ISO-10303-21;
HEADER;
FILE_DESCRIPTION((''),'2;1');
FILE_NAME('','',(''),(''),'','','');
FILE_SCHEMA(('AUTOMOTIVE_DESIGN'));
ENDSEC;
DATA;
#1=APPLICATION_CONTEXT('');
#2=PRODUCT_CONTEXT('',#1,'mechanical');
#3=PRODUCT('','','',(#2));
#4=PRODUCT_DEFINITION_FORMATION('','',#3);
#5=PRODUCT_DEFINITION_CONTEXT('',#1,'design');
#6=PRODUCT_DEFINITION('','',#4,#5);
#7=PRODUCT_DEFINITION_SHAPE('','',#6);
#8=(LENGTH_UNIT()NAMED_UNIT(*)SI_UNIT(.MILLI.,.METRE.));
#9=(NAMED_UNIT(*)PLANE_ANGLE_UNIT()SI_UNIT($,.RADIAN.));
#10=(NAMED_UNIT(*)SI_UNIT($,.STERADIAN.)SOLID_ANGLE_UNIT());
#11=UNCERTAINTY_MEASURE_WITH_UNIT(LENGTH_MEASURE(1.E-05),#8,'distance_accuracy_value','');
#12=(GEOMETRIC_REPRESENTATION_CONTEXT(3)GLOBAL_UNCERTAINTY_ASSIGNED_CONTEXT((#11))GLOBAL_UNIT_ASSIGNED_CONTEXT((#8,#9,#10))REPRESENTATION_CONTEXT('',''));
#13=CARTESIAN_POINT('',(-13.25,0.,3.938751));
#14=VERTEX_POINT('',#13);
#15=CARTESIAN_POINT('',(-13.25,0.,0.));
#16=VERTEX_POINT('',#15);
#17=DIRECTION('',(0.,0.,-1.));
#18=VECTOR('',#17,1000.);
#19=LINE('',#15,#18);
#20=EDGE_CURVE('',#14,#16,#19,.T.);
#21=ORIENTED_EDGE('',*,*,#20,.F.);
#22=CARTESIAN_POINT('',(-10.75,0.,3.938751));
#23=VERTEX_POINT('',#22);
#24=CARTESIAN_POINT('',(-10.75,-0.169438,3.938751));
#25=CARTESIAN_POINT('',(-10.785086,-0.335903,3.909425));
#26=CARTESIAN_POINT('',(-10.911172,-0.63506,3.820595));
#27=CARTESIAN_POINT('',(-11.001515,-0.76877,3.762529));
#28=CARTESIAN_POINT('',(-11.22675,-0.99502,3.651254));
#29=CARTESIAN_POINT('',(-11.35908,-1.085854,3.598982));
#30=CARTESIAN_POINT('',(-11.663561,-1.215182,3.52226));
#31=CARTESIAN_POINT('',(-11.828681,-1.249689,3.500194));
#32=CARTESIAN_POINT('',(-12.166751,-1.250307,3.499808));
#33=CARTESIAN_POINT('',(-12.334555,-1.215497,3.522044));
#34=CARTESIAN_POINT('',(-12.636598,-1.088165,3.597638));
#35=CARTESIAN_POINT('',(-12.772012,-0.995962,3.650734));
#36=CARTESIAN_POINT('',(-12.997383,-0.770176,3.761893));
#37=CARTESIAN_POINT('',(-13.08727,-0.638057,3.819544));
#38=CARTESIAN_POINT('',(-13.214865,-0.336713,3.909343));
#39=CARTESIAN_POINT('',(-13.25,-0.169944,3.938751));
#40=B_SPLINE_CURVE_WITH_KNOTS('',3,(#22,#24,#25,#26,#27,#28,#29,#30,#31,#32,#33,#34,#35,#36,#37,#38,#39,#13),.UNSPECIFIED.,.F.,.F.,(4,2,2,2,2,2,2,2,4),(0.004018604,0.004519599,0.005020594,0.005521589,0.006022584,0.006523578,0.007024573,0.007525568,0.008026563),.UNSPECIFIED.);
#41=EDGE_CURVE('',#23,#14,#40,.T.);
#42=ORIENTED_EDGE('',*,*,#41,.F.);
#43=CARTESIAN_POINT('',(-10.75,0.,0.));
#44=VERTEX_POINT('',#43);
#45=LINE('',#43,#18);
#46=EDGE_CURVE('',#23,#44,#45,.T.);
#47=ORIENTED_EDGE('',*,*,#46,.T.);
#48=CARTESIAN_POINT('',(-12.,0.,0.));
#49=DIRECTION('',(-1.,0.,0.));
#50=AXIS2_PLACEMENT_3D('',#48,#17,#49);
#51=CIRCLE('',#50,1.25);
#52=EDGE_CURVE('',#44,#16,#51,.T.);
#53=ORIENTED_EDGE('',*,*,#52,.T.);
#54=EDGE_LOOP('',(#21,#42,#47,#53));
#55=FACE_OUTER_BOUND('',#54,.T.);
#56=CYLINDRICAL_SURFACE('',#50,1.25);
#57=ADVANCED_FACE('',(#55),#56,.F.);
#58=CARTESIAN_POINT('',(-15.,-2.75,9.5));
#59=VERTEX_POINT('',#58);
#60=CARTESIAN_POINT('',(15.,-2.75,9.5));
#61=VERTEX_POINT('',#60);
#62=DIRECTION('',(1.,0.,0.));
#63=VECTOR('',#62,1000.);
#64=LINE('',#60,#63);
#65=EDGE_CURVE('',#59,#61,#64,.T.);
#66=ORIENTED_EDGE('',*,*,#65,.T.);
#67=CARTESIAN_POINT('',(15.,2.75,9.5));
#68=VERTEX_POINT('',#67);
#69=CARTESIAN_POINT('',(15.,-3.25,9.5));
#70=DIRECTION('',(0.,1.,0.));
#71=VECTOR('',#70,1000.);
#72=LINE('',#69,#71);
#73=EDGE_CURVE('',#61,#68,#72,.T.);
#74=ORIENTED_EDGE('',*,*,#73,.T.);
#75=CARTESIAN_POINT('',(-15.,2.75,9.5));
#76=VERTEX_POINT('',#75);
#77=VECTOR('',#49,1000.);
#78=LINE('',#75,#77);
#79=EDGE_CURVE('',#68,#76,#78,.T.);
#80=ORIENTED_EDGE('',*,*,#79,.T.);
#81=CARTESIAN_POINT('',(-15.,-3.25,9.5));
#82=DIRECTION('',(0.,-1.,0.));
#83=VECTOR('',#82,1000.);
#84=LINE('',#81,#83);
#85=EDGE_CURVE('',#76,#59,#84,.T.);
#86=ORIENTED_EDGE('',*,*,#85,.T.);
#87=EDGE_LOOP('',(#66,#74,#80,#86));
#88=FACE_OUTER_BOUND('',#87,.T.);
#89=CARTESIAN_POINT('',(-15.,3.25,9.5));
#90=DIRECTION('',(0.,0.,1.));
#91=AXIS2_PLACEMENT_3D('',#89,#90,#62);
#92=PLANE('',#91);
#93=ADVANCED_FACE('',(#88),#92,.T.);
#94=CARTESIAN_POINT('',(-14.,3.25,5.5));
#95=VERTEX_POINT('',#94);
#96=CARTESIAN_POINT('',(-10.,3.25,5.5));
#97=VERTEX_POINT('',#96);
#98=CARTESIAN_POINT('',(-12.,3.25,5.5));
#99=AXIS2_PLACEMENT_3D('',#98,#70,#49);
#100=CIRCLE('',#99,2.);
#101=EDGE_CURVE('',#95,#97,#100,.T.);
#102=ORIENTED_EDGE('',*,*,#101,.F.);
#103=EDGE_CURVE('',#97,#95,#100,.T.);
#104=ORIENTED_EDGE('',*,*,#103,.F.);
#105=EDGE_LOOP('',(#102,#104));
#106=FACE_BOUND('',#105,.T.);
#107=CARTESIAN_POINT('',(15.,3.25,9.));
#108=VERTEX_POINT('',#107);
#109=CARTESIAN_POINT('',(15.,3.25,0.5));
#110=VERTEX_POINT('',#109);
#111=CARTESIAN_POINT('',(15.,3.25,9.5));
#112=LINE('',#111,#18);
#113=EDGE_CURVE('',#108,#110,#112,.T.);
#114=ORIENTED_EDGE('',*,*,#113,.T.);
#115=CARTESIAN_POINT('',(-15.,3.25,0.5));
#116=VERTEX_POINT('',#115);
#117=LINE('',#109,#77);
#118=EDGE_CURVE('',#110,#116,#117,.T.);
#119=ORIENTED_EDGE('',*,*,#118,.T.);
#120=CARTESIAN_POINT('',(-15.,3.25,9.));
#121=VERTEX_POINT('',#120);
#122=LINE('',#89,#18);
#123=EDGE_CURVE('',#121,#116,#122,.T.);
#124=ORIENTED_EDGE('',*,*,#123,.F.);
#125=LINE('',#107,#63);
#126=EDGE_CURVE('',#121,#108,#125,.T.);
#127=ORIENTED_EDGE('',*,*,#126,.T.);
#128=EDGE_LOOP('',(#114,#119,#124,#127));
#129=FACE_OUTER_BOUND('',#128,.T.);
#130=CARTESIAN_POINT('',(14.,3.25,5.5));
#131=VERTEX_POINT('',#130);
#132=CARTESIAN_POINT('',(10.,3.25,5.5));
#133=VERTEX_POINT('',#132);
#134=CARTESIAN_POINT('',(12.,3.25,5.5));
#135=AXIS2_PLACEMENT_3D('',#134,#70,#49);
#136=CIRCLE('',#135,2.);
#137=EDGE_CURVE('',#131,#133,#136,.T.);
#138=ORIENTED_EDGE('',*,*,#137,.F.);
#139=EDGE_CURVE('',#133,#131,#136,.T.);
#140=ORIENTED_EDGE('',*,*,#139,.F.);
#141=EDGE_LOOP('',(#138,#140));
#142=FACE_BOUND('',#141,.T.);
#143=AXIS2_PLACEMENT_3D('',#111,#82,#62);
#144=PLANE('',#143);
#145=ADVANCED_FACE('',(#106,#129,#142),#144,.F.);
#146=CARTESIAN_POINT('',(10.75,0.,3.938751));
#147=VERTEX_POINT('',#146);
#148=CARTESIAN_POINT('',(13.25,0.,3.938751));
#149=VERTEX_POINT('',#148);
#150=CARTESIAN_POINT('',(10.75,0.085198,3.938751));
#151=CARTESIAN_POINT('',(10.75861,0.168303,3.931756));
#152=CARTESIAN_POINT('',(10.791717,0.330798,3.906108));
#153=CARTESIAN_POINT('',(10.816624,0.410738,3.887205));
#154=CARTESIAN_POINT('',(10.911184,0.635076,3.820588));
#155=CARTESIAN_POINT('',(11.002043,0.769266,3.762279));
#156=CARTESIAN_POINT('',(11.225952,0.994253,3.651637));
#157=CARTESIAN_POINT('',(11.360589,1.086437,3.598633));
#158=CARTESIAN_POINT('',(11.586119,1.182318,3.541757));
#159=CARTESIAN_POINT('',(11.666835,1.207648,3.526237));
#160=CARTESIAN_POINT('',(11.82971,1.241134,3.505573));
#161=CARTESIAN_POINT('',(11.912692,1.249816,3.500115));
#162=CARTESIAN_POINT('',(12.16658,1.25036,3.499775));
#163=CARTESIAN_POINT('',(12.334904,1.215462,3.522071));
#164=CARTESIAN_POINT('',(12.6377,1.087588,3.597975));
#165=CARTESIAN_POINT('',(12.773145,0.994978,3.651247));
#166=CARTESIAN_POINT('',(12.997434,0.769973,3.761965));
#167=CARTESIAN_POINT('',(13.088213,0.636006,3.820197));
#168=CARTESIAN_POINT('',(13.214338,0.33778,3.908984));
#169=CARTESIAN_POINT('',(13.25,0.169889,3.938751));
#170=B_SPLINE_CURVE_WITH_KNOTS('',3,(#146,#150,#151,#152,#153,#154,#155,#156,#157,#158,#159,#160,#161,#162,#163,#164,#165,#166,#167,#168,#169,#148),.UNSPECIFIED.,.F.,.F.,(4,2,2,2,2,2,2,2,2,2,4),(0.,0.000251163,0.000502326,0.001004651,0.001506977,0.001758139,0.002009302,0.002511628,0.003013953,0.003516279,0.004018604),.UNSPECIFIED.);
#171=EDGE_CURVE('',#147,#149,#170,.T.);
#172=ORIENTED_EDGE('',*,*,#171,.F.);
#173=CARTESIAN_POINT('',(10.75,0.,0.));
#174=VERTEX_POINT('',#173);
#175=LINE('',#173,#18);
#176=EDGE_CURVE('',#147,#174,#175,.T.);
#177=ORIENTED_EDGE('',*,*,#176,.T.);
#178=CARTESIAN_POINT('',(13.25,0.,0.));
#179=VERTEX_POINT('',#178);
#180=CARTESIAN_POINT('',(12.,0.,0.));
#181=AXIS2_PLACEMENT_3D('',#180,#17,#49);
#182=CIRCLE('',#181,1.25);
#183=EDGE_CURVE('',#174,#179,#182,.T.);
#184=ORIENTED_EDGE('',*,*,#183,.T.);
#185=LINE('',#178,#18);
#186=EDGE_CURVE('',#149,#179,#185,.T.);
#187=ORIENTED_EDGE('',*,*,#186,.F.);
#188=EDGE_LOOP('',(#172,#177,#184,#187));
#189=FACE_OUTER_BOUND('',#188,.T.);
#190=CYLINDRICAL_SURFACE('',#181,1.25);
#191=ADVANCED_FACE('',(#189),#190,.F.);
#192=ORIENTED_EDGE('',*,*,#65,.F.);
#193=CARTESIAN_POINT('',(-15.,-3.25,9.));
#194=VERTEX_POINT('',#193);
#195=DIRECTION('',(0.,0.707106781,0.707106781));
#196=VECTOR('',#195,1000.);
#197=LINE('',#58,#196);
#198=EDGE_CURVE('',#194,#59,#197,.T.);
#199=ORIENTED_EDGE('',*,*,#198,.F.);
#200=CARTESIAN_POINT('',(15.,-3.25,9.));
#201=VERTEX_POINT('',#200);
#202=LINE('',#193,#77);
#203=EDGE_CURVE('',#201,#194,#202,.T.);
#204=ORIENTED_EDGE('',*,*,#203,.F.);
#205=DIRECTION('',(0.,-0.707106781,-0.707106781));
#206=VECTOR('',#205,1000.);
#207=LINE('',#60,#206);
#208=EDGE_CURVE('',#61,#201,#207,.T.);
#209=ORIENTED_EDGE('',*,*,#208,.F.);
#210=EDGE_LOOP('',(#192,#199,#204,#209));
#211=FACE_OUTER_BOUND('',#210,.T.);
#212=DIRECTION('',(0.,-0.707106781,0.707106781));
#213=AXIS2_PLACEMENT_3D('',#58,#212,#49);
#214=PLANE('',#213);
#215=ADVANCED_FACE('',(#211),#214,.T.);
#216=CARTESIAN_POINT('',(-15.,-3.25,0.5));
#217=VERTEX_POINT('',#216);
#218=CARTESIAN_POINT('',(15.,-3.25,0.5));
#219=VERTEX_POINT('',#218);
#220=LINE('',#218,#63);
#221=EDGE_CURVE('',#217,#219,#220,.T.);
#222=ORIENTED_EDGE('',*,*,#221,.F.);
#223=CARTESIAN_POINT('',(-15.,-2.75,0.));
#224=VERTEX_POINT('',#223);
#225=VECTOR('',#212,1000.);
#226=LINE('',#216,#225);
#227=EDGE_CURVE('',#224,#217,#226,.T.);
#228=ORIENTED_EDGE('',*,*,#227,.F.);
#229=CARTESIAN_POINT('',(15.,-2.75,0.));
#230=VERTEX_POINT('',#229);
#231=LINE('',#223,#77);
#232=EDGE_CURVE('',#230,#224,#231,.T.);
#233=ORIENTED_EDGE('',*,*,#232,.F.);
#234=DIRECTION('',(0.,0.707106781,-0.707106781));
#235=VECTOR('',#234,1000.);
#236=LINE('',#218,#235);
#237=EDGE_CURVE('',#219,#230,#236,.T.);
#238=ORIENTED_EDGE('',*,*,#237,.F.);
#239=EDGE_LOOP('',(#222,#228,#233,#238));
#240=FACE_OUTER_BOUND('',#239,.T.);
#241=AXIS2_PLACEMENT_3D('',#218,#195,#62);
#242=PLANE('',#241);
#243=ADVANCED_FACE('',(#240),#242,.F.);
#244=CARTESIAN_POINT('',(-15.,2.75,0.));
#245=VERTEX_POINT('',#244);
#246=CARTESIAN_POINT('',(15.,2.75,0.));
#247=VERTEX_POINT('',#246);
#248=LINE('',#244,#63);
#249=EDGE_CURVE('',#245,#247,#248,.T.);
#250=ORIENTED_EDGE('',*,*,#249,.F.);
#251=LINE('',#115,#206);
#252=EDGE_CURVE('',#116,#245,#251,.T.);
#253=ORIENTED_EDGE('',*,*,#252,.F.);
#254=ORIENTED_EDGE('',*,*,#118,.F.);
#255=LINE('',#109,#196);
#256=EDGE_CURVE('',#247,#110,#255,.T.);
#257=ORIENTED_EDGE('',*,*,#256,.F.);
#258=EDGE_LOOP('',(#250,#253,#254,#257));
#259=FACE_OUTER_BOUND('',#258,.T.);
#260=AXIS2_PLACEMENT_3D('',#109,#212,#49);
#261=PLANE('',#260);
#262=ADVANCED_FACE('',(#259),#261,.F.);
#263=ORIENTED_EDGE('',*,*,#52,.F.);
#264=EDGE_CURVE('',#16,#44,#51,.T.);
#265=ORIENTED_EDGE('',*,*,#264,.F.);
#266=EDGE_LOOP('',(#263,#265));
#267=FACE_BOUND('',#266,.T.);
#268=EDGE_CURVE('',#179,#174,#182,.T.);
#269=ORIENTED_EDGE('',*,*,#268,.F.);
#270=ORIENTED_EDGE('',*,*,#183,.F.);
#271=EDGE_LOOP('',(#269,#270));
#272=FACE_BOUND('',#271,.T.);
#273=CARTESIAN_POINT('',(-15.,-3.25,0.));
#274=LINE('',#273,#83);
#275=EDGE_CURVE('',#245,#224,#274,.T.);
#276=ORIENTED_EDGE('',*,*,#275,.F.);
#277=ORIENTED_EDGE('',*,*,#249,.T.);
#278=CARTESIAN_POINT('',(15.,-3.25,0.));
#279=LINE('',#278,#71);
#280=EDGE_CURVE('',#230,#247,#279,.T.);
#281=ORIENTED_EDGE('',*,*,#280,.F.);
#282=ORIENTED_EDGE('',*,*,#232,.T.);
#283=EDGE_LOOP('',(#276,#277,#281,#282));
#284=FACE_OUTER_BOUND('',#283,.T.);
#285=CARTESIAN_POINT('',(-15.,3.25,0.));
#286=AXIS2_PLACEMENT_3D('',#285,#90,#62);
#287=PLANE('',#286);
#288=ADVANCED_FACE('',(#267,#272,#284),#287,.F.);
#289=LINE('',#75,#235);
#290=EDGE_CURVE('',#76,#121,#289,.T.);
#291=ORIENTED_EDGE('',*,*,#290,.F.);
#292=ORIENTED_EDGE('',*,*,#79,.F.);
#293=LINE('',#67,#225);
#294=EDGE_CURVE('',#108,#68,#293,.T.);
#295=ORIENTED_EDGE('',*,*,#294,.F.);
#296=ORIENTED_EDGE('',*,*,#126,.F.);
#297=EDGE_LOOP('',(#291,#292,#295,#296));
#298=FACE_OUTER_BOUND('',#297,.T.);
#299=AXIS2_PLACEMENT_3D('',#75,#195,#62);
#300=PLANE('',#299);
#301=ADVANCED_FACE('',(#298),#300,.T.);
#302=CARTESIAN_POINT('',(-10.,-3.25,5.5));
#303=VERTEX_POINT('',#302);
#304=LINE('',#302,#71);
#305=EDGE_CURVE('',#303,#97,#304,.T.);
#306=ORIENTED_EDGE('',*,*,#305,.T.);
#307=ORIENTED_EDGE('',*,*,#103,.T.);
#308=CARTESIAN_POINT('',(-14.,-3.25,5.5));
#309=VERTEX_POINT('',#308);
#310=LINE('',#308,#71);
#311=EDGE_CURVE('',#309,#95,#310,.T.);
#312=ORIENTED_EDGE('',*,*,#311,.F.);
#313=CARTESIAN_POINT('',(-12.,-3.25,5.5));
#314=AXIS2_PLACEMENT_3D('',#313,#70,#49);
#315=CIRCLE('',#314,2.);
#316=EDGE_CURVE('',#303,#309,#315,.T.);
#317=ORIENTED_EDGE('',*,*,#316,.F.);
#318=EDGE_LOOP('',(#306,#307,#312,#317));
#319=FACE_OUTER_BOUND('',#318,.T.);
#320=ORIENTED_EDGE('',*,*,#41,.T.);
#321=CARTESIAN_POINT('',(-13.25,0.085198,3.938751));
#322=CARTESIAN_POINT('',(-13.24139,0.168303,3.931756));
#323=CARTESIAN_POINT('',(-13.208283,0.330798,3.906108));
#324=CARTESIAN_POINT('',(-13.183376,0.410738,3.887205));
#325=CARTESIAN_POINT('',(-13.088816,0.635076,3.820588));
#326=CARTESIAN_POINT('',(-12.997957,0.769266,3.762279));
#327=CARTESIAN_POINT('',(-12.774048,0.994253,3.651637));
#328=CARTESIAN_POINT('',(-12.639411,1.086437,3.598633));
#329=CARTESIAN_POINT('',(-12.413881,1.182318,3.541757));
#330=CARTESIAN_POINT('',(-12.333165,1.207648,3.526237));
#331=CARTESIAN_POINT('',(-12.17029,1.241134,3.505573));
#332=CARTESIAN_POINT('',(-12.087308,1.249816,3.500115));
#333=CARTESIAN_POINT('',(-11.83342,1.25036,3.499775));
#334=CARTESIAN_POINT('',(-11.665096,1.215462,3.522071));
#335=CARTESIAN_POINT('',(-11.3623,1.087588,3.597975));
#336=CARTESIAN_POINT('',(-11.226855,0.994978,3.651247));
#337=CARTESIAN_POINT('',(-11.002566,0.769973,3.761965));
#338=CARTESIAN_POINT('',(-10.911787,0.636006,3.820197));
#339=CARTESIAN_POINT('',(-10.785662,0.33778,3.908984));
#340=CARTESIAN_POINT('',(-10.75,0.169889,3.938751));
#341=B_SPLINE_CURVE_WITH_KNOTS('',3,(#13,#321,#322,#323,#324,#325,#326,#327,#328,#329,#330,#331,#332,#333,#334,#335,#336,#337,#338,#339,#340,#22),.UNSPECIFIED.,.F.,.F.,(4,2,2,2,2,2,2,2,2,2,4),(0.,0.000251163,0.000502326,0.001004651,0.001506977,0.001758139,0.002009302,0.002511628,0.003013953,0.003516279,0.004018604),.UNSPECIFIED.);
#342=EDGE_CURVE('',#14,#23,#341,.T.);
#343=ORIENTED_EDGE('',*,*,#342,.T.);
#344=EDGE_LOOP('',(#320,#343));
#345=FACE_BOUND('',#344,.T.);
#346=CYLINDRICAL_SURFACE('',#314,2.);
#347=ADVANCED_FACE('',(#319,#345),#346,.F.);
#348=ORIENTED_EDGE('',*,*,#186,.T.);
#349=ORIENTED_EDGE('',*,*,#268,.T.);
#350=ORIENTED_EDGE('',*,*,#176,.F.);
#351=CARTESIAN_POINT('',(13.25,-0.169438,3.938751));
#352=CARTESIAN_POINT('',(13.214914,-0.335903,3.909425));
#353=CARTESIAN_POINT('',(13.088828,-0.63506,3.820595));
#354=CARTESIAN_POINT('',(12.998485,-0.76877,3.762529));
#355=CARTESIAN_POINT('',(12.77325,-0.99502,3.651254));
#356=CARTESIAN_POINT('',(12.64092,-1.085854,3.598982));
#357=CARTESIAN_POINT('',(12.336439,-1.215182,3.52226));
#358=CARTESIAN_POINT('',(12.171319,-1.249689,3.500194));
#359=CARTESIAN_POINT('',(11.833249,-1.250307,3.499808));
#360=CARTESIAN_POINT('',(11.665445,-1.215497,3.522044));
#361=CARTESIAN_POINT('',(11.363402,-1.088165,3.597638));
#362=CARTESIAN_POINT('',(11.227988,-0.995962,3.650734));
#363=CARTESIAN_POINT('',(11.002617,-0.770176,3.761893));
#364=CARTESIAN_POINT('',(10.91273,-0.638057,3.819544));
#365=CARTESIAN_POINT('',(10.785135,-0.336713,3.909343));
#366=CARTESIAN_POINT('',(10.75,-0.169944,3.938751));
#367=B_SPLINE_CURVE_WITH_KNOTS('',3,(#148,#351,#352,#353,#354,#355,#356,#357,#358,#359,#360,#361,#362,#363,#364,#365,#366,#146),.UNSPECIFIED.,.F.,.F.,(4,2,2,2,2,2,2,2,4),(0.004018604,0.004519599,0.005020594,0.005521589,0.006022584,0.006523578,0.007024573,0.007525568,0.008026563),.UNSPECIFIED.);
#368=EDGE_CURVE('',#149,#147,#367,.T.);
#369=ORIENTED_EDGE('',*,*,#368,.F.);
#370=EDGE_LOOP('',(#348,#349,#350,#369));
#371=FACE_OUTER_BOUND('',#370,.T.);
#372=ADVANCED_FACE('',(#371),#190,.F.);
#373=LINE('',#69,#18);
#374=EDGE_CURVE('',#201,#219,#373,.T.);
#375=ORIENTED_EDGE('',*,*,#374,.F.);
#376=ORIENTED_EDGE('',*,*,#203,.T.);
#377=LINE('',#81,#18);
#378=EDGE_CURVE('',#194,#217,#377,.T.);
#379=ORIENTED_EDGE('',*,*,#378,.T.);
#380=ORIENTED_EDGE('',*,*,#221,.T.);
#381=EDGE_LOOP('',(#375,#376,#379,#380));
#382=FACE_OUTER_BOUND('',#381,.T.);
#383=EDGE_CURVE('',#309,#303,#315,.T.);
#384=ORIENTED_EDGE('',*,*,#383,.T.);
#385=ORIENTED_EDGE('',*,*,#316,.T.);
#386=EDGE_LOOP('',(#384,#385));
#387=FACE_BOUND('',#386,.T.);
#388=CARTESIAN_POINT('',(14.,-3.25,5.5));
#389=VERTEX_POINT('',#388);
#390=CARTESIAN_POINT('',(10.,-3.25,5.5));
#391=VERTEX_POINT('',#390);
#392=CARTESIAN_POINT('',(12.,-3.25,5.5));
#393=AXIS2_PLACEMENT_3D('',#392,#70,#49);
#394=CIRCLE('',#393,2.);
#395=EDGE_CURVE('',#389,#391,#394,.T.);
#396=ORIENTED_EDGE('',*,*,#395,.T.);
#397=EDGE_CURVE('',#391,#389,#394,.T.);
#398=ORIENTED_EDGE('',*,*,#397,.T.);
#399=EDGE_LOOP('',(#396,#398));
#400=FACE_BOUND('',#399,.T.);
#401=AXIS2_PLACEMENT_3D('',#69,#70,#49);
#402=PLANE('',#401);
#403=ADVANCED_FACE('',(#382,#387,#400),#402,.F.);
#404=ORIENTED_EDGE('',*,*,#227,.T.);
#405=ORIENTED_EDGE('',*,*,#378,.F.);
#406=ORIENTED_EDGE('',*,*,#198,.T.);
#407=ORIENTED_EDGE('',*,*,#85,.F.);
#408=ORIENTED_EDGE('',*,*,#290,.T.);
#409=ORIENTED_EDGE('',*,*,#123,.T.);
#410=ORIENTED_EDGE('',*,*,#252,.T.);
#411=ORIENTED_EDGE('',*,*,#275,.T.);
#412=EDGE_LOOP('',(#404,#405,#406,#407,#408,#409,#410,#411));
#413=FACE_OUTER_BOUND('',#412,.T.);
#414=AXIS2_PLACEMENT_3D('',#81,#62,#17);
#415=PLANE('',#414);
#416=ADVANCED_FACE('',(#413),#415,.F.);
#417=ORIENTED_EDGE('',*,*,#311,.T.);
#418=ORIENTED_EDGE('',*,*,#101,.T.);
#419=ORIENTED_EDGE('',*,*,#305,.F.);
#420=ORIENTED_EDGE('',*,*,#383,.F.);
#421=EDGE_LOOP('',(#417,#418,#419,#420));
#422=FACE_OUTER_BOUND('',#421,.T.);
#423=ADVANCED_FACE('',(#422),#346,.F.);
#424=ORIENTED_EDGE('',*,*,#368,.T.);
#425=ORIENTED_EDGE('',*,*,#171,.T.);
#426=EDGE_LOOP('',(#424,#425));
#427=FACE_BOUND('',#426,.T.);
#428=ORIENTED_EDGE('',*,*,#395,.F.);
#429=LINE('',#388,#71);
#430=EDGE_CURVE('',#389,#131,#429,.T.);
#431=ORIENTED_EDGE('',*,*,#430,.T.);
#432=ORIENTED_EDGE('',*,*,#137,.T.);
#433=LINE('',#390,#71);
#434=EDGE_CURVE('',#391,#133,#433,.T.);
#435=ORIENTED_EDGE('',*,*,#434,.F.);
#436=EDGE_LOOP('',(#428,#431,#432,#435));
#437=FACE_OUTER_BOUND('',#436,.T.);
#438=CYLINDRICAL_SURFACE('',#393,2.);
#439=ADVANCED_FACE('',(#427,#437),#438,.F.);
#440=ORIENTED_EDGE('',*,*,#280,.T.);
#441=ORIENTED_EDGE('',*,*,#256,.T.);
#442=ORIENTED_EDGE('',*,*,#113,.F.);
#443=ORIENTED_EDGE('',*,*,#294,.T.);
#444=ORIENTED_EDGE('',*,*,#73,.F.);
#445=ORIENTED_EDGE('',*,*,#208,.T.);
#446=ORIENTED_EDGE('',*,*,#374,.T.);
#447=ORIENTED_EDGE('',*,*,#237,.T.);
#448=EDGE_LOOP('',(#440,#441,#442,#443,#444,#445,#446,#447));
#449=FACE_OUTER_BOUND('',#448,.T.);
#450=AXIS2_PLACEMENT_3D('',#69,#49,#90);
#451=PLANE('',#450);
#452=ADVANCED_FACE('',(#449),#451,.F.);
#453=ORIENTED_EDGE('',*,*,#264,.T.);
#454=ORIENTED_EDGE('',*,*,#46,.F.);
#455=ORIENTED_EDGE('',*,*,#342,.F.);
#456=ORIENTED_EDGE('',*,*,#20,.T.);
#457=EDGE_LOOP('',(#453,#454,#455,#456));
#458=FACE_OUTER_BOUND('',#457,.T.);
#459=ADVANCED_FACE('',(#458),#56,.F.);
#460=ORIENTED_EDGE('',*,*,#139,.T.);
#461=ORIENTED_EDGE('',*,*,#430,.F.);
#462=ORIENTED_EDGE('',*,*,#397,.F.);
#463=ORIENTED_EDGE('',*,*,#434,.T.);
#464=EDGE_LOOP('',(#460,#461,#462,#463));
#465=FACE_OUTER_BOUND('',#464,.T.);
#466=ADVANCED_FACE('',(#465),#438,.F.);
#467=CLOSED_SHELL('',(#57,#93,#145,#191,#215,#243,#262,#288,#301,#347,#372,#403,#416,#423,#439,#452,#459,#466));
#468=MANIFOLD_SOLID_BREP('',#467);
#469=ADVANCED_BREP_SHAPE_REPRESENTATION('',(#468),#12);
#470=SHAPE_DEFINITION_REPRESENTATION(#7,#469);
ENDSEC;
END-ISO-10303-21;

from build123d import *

# Parameters (mm, degrees)
SKETCH1_W              = 30
SKETCH1_H              = 6.5
BOSS_EXTRUDE1_DEPTH    = 9.5
SKETCH2_R              = 2
CUT_EXTRUDE1_DEPTH     = 19.907670401
M3_TAPPED_HOLE1_REACH  = 20.05
M3_TAPPED_HOLE1_BORE_R = 1.25
CHAMFER1_SIZE          = 0.5


with BuildPart() as part:
    # Sketch1 → Boss-Extrude1 (new body)
    with BuildSketch(Plane.XY):
        Rectangle(SKETCH1_W, SKETCH1_H)
    extrude(amount=BOSS_EXTRUDE1_DEPTH)

    # Sketch2 → Cut-Extrude1 (cut, through all)
    with BuildSketch(Plane(origin=(0, 3.25, 0), x_dir=(1, 0, 0), z_dir=(0, 1, 0))):
        with Locations(Location((-12, -5.5, 0), (0, 0, 180))):
            Circle(SKETCH2_R)
        with Locations(Location((12, -5.5, 0), (0, 0, 180))):
            Circle(SKETCH2_R)
    extrude(amount=-CUT_EXTRUDE1_DEPTH, mode=Mode.SUBTRACT)

    # M3 Tapped Hole1 bore → M3 Tapped Hole1 (cut, up to next)
    with BuildSketch(Plane(origin=(0, 0, 0), x_dir=(-1, 0, 0), z_dir=(0, 0, -1)), mode=Mode.PRIVATE) as m3_tapped_hole1_sk1:
        with Locations((12, 0)):
            Circle(M3_TAPPED_HOLE1_BORE_R)
    m3_tapped_hole1_tool1 = extrude(m3_tapped_hole1_sk1.sketch, amount=-M3_TAPPED_HOLE1_REACH, mode=Mode.PRIVATE) & part.part
    # M3 Tapped Hole1 bore → M3 Tapped Hole1 (cut, up to next)
    with BuildSketch(Plane(origin=(0, 0, 0), x_dir=(-1, 0, 0), z_dir=(0, 0, -1)), mode=Mode.PRIVATE) as m3_tapped_hole1_sk2:
        with Locations((-12, 0)):
            Circle(M3_TAPPED_HOLE1_BORE_R)
    m3_tapped_hole1_tool2 = extrude(m3_tapped_hole1_sk2.sketch, amount=-M3_TAPPED_HOLE1_REACH, mode=Mode.PRIVATE) & part.part
    add(m3_tapped_hole1_tool1.solids().sort_by_distance((-12, 0, 0))[0], mode=Mode.SUBTRACT)
    add(m3_tapped_hole1_tool2.solids().sort_by_distance((12, 0, 0))[0], mode=Mode.SUBTRACT)

    # Chamfer1
    chamfer1_edges = [part.edges().sort_by_distance(p)[0] for p in [
        (0, 3.25, 9.5),
        (0, 3.25, 0),
        (0, -3.25, 0),
        (0, -3.25, 9.5),
    ]]
    chamfer(chamfer1_edges, length=CHAMFER1_SIZE)


solid = part.part
